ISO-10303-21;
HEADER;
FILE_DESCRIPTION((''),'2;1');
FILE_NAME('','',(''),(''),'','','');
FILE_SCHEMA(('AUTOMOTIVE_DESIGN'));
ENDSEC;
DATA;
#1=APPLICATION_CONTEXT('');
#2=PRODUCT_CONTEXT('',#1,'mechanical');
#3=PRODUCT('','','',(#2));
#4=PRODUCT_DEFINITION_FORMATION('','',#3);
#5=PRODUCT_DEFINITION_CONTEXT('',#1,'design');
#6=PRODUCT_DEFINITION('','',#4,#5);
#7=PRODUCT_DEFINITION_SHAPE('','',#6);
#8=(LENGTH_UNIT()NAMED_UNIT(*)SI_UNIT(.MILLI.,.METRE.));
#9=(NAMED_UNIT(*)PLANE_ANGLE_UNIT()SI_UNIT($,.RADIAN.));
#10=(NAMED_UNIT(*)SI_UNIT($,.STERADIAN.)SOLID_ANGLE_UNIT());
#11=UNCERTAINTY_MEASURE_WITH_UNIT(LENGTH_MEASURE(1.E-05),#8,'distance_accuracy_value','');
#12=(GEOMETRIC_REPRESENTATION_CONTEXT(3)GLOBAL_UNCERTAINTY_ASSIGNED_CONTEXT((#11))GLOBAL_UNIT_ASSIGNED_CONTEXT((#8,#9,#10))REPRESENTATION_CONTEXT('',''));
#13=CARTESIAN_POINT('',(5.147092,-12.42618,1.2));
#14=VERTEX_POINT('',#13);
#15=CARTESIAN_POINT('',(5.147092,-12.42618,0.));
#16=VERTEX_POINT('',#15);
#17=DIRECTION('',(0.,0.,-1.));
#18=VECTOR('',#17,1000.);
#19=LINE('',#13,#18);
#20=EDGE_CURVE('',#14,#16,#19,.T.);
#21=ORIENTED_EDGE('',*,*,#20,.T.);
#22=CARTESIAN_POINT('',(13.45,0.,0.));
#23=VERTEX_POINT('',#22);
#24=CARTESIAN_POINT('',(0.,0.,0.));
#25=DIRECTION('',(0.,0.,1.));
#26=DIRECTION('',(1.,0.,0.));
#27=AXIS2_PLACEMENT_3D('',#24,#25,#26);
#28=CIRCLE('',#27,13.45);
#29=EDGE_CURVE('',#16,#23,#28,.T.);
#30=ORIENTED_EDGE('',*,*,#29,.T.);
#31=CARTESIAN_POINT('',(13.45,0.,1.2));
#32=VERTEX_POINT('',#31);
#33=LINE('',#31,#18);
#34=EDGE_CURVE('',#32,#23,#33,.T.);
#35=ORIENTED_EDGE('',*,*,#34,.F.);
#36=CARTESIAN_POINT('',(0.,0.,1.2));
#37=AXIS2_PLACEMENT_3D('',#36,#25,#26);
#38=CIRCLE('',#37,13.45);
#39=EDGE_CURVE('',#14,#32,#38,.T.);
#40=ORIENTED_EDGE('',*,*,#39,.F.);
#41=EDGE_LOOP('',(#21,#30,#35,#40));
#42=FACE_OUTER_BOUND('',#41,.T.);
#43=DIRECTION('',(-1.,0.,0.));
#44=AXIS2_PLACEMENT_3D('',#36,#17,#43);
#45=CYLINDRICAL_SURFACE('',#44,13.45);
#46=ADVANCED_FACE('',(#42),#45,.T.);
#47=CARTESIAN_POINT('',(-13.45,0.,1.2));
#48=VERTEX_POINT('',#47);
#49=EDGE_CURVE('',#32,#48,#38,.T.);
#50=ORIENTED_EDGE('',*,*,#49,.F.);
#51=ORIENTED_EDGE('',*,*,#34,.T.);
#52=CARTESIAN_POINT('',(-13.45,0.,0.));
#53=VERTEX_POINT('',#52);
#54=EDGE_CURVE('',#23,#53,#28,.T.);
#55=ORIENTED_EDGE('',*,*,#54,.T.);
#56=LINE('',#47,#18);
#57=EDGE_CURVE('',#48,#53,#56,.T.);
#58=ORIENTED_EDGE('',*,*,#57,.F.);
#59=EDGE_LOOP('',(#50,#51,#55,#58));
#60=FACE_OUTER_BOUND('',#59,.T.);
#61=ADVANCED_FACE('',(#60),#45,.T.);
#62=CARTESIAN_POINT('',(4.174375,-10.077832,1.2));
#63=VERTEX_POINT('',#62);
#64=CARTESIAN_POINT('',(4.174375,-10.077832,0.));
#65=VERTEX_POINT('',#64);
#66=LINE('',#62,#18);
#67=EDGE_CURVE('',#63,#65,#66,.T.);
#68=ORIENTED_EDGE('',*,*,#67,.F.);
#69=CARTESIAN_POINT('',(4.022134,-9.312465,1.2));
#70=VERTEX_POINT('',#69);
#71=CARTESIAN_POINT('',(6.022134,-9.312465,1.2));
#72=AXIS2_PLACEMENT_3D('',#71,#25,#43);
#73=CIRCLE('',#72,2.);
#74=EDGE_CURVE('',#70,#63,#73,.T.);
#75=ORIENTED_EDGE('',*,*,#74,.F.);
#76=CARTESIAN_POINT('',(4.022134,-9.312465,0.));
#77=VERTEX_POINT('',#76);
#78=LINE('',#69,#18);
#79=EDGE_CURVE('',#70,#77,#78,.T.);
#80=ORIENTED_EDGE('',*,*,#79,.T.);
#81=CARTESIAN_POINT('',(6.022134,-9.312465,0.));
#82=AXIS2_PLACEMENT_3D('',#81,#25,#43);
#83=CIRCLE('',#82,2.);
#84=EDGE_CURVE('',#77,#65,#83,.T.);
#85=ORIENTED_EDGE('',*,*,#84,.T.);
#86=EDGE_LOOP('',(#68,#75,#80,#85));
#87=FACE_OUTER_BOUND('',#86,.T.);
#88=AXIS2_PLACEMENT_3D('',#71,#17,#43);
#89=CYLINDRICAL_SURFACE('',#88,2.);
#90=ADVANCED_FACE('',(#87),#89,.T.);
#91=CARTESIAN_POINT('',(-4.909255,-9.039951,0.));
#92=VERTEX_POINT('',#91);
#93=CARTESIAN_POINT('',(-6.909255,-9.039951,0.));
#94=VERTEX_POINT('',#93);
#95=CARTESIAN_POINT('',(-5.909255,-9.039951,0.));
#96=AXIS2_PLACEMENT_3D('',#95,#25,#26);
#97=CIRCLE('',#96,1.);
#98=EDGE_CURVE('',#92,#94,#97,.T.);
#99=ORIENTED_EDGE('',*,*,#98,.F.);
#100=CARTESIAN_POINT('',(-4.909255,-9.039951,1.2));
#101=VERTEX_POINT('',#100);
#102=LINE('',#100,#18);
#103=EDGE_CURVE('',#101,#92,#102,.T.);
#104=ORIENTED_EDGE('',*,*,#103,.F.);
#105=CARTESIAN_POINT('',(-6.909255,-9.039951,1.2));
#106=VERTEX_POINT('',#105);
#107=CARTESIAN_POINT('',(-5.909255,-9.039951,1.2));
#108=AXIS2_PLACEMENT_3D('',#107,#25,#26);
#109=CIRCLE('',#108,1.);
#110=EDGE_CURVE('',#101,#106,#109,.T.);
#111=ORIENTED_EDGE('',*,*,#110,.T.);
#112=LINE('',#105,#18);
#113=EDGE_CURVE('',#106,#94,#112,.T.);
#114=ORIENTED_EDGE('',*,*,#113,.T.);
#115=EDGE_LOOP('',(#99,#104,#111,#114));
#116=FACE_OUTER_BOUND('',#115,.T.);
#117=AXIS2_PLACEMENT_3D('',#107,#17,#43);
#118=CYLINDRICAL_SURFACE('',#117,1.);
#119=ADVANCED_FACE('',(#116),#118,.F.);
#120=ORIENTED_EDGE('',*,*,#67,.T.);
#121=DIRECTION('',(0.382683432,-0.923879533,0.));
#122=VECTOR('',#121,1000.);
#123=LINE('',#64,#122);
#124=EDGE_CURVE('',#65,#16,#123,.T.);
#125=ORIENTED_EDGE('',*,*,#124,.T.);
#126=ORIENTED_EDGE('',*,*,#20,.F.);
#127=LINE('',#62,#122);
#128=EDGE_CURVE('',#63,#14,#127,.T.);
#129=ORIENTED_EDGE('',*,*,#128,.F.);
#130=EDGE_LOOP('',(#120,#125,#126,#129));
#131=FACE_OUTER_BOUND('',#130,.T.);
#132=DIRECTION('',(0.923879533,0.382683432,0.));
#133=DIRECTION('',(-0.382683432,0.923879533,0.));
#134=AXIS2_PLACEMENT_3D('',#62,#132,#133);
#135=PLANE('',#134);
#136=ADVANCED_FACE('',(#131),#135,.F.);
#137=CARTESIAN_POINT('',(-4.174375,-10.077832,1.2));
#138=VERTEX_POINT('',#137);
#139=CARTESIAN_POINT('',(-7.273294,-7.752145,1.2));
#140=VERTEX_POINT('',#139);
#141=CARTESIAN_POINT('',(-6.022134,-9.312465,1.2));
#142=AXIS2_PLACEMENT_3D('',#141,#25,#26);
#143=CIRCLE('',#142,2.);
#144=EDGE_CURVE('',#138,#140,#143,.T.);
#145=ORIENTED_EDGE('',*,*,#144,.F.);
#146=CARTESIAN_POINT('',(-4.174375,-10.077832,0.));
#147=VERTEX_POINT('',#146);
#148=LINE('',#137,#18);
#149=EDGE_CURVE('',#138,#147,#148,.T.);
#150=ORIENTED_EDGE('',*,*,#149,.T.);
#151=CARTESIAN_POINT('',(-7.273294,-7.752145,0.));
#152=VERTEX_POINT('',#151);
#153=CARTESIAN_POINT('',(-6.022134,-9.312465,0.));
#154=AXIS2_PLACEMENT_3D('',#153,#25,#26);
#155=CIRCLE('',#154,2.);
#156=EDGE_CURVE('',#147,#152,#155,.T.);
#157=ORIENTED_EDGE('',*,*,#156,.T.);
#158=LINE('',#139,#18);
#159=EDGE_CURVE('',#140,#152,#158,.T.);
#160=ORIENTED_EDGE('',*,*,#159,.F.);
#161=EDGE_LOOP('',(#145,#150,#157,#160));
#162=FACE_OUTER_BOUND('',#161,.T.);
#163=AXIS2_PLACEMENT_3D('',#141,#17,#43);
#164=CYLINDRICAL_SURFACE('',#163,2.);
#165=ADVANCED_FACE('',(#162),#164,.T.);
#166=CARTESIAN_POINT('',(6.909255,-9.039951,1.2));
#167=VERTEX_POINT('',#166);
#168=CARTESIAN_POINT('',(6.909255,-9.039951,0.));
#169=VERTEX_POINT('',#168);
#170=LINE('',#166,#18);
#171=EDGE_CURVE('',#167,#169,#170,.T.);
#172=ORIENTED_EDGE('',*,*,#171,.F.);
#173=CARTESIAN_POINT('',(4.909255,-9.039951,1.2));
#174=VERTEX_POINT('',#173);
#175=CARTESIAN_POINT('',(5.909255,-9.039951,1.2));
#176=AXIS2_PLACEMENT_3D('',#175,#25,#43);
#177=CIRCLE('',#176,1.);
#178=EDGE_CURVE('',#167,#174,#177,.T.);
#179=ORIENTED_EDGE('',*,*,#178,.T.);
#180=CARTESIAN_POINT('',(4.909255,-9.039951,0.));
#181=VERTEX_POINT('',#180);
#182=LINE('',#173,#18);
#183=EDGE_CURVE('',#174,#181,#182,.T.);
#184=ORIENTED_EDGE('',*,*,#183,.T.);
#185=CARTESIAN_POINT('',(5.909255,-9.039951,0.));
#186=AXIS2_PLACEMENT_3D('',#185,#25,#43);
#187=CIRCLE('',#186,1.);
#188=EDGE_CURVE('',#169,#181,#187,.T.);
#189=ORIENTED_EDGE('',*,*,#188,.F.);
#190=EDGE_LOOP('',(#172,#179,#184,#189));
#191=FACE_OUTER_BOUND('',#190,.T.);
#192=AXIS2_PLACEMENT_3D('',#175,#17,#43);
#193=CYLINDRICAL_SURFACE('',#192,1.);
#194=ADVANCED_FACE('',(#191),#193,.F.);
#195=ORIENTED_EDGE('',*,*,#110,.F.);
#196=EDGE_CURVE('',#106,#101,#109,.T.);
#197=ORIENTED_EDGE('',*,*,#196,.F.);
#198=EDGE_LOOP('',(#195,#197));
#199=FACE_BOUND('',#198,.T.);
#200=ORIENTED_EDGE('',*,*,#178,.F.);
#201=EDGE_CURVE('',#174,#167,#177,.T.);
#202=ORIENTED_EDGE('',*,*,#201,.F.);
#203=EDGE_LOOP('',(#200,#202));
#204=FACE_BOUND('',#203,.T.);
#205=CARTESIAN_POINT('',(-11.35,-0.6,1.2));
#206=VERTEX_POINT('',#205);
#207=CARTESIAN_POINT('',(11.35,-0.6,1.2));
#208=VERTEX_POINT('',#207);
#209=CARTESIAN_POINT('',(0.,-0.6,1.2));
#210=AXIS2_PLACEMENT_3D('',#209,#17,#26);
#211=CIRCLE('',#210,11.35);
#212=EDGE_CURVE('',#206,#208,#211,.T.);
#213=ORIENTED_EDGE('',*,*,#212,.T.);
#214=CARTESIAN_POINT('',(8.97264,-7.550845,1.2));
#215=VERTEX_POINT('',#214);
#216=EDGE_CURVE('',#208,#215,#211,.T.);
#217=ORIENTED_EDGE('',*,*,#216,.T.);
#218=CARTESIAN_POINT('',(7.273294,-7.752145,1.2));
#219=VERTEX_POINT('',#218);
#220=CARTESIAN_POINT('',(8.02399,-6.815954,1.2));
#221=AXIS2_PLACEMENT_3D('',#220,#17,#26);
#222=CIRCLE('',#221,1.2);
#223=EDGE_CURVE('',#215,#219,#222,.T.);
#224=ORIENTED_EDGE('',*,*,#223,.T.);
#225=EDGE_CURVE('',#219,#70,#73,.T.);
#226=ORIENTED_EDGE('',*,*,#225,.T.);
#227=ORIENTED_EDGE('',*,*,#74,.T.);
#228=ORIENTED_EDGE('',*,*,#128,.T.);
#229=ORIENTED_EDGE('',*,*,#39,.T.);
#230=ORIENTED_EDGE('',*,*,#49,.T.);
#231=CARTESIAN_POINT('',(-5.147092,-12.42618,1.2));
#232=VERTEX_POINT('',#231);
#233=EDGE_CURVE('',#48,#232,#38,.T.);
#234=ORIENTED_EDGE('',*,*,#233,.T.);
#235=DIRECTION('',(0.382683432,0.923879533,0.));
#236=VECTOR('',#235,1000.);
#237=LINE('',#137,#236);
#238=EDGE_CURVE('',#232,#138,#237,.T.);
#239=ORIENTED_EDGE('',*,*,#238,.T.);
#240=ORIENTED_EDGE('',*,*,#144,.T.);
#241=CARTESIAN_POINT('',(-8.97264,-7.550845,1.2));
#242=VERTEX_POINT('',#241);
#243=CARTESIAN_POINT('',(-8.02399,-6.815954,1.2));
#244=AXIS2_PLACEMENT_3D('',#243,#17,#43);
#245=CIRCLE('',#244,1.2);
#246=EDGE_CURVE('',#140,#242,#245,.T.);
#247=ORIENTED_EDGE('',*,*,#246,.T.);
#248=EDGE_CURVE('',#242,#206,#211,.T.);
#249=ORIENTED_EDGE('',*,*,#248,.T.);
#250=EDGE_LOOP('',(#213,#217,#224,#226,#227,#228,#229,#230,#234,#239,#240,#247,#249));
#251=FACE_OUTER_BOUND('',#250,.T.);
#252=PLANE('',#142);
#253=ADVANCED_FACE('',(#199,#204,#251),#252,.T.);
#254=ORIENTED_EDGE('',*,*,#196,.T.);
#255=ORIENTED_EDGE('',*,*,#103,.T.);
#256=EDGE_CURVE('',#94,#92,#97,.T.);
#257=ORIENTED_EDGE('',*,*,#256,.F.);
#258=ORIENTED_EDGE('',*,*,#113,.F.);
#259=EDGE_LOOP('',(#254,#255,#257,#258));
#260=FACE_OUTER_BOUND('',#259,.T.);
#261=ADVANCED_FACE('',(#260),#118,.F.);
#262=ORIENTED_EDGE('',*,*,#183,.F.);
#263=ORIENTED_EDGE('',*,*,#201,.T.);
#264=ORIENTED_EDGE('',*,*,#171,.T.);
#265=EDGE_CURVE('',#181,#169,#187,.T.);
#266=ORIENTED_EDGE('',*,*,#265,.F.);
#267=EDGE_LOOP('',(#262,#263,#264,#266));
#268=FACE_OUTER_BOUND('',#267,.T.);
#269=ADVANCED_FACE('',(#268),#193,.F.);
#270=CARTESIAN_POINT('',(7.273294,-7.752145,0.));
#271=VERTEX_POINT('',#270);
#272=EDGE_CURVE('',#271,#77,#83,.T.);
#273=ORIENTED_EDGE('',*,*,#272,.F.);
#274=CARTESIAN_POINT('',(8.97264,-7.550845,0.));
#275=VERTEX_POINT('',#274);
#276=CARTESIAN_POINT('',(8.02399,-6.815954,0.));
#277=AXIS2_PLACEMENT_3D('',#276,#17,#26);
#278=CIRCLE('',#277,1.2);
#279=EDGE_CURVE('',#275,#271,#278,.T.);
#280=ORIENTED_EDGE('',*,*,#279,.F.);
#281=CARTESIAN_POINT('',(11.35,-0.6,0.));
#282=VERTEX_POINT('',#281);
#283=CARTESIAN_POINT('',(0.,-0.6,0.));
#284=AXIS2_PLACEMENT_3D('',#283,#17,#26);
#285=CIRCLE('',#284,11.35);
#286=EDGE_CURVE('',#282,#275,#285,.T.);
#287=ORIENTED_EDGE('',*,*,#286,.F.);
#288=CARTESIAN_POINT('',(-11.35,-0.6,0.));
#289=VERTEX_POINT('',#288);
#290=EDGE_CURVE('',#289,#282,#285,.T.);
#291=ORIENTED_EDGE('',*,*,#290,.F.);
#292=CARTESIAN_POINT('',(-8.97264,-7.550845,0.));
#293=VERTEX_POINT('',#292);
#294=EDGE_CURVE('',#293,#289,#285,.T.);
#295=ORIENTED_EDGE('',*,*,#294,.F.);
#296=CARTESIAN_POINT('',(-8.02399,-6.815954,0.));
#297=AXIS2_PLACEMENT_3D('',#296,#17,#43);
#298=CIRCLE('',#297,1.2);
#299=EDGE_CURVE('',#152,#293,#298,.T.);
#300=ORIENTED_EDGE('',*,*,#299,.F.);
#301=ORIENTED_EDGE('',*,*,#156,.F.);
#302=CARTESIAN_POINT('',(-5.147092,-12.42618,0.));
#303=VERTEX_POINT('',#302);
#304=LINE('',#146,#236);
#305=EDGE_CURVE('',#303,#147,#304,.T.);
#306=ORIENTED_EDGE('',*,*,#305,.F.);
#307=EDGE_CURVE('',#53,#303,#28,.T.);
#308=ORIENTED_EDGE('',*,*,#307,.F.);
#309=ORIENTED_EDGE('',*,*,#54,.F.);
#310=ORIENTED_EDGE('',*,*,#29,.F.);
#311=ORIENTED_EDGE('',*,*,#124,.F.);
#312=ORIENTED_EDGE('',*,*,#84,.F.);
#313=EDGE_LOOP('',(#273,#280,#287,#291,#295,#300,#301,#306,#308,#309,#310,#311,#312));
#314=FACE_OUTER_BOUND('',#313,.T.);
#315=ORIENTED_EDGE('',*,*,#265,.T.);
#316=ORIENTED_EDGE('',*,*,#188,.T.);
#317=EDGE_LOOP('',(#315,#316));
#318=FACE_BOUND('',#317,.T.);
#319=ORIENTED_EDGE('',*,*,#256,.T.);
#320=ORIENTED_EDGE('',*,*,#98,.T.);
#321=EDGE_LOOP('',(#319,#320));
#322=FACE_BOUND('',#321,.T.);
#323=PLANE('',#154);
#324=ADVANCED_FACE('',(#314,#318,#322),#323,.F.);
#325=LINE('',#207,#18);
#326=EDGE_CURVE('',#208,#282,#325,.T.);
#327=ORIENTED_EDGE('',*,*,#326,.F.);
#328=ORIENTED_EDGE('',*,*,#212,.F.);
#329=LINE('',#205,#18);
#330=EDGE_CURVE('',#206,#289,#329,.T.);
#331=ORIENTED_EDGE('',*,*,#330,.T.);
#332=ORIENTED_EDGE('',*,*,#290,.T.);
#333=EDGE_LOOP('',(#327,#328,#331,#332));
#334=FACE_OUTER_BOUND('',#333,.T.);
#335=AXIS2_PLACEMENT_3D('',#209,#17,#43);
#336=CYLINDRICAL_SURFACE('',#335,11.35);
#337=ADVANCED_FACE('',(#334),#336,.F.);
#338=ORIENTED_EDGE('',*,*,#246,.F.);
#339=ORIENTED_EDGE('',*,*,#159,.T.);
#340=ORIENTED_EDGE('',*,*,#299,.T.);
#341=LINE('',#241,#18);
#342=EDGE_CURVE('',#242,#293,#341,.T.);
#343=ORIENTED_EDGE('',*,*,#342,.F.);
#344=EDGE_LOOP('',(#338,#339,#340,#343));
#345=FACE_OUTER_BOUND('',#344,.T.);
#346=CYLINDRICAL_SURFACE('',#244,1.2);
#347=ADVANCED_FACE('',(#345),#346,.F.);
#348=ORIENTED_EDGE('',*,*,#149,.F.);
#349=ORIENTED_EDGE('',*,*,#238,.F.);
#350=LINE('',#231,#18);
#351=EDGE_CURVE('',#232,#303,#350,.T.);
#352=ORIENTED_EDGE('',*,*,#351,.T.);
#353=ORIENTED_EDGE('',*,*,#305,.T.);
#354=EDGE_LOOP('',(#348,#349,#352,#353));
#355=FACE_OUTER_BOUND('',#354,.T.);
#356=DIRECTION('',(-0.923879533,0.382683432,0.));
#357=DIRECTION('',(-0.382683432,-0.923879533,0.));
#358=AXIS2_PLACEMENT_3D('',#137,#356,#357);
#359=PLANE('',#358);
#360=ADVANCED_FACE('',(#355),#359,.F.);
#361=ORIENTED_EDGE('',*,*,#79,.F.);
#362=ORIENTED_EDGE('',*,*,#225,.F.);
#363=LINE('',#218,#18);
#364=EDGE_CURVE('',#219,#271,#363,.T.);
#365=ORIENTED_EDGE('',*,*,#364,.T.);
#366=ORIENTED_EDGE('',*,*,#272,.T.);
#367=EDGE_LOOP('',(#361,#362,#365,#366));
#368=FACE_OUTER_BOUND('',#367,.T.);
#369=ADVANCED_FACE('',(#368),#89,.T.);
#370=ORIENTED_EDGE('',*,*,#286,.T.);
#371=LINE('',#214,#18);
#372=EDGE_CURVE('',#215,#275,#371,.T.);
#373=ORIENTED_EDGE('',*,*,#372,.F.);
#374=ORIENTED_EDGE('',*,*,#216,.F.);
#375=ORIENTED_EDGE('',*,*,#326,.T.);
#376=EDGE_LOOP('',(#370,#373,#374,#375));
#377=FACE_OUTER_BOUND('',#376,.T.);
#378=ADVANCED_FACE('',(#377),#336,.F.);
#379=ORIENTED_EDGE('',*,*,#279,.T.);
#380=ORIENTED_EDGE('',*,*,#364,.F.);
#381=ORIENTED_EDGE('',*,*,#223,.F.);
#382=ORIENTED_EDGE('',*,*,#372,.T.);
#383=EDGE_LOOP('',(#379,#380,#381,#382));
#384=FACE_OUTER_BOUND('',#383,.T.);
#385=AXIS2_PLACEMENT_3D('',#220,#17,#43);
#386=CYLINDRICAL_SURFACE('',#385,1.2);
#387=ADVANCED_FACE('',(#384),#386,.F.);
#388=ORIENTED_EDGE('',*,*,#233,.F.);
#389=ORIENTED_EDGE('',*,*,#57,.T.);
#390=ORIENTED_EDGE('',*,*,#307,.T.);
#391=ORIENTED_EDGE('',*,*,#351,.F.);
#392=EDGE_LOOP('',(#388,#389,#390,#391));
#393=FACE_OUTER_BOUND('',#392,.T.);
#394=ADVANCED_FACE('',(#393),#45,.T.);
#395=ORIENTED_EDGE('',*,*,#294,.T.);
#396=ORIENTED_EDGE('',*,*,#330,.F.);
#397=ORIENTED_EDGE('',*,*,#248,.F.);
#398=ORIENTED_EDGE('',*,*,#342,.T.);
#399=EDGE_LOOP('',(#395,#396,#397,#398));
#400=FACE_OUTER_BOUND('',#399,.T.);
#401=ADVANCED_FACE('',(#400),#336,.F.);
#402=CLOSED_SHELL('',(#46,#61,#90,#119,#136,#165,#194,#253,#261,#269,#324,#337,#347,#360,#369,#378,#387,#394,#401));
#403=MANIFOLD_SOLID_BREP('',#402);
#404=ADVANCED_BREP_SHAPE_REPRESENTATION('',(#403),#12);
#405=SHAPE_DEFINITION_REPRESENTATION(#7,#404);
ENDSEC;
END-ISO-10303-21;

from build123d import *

# Parameters (mm, degrees)
SKETCH1_R          = 1
BASE_EXTRUDE_DEPTH = 1.2


with BuildPart() as part:
    # Sketch1 → Base-Extrude (new body)
    with BuildSketch(Plane.XY):
        with BuildLine():
            Line((-4.17437466, -10.077831919), (-5.147092165, -12.426179712))
            ThreePointArc((-5.147092165, -12.426179712), (0, 13.45), (5.147092165, -12.426179712))
            Line((5.147092165, -12.426179712), (4.17437466, -10.077831919))
            ThreePointArc((4.17437466, -10.077831919), (4.821639244, -7.712836035), (7.273294145, -7.752145343))
            ThreePointArc((7.273294145, -7.752145343), (8.165152835, -8.007621744), (8.972639508, -7.550844571))
            ThreePointArc((8.972639508, -7.550844571), (0, 10.75), (-8.972639508, -7.550844571))
            ThreePointArc((-8.972639508, -7.550844571), (-8.165152835, -8.007621744), (-7.273294145, -7.752145343))
            ThreePointArc((-7.273294145, -7.752145343), (-4.821639244, -7.712836035), (-4.17437466, -10.077831919))
        make_face()
        with Locations((-5.909254613, -9.03995077)):
            Circle(SKETCH1_R, mode=Mode.SUBTRACT)
        with Locations(Location((5.909254613, -9.03995077, 0), (0, 0, 180))):
            Circle(SKETCH1_R, mode=Mode.SUBTRACT)
    extrude(amount=BASE_EXTRUDE_DEPTH)


solid = part.part
